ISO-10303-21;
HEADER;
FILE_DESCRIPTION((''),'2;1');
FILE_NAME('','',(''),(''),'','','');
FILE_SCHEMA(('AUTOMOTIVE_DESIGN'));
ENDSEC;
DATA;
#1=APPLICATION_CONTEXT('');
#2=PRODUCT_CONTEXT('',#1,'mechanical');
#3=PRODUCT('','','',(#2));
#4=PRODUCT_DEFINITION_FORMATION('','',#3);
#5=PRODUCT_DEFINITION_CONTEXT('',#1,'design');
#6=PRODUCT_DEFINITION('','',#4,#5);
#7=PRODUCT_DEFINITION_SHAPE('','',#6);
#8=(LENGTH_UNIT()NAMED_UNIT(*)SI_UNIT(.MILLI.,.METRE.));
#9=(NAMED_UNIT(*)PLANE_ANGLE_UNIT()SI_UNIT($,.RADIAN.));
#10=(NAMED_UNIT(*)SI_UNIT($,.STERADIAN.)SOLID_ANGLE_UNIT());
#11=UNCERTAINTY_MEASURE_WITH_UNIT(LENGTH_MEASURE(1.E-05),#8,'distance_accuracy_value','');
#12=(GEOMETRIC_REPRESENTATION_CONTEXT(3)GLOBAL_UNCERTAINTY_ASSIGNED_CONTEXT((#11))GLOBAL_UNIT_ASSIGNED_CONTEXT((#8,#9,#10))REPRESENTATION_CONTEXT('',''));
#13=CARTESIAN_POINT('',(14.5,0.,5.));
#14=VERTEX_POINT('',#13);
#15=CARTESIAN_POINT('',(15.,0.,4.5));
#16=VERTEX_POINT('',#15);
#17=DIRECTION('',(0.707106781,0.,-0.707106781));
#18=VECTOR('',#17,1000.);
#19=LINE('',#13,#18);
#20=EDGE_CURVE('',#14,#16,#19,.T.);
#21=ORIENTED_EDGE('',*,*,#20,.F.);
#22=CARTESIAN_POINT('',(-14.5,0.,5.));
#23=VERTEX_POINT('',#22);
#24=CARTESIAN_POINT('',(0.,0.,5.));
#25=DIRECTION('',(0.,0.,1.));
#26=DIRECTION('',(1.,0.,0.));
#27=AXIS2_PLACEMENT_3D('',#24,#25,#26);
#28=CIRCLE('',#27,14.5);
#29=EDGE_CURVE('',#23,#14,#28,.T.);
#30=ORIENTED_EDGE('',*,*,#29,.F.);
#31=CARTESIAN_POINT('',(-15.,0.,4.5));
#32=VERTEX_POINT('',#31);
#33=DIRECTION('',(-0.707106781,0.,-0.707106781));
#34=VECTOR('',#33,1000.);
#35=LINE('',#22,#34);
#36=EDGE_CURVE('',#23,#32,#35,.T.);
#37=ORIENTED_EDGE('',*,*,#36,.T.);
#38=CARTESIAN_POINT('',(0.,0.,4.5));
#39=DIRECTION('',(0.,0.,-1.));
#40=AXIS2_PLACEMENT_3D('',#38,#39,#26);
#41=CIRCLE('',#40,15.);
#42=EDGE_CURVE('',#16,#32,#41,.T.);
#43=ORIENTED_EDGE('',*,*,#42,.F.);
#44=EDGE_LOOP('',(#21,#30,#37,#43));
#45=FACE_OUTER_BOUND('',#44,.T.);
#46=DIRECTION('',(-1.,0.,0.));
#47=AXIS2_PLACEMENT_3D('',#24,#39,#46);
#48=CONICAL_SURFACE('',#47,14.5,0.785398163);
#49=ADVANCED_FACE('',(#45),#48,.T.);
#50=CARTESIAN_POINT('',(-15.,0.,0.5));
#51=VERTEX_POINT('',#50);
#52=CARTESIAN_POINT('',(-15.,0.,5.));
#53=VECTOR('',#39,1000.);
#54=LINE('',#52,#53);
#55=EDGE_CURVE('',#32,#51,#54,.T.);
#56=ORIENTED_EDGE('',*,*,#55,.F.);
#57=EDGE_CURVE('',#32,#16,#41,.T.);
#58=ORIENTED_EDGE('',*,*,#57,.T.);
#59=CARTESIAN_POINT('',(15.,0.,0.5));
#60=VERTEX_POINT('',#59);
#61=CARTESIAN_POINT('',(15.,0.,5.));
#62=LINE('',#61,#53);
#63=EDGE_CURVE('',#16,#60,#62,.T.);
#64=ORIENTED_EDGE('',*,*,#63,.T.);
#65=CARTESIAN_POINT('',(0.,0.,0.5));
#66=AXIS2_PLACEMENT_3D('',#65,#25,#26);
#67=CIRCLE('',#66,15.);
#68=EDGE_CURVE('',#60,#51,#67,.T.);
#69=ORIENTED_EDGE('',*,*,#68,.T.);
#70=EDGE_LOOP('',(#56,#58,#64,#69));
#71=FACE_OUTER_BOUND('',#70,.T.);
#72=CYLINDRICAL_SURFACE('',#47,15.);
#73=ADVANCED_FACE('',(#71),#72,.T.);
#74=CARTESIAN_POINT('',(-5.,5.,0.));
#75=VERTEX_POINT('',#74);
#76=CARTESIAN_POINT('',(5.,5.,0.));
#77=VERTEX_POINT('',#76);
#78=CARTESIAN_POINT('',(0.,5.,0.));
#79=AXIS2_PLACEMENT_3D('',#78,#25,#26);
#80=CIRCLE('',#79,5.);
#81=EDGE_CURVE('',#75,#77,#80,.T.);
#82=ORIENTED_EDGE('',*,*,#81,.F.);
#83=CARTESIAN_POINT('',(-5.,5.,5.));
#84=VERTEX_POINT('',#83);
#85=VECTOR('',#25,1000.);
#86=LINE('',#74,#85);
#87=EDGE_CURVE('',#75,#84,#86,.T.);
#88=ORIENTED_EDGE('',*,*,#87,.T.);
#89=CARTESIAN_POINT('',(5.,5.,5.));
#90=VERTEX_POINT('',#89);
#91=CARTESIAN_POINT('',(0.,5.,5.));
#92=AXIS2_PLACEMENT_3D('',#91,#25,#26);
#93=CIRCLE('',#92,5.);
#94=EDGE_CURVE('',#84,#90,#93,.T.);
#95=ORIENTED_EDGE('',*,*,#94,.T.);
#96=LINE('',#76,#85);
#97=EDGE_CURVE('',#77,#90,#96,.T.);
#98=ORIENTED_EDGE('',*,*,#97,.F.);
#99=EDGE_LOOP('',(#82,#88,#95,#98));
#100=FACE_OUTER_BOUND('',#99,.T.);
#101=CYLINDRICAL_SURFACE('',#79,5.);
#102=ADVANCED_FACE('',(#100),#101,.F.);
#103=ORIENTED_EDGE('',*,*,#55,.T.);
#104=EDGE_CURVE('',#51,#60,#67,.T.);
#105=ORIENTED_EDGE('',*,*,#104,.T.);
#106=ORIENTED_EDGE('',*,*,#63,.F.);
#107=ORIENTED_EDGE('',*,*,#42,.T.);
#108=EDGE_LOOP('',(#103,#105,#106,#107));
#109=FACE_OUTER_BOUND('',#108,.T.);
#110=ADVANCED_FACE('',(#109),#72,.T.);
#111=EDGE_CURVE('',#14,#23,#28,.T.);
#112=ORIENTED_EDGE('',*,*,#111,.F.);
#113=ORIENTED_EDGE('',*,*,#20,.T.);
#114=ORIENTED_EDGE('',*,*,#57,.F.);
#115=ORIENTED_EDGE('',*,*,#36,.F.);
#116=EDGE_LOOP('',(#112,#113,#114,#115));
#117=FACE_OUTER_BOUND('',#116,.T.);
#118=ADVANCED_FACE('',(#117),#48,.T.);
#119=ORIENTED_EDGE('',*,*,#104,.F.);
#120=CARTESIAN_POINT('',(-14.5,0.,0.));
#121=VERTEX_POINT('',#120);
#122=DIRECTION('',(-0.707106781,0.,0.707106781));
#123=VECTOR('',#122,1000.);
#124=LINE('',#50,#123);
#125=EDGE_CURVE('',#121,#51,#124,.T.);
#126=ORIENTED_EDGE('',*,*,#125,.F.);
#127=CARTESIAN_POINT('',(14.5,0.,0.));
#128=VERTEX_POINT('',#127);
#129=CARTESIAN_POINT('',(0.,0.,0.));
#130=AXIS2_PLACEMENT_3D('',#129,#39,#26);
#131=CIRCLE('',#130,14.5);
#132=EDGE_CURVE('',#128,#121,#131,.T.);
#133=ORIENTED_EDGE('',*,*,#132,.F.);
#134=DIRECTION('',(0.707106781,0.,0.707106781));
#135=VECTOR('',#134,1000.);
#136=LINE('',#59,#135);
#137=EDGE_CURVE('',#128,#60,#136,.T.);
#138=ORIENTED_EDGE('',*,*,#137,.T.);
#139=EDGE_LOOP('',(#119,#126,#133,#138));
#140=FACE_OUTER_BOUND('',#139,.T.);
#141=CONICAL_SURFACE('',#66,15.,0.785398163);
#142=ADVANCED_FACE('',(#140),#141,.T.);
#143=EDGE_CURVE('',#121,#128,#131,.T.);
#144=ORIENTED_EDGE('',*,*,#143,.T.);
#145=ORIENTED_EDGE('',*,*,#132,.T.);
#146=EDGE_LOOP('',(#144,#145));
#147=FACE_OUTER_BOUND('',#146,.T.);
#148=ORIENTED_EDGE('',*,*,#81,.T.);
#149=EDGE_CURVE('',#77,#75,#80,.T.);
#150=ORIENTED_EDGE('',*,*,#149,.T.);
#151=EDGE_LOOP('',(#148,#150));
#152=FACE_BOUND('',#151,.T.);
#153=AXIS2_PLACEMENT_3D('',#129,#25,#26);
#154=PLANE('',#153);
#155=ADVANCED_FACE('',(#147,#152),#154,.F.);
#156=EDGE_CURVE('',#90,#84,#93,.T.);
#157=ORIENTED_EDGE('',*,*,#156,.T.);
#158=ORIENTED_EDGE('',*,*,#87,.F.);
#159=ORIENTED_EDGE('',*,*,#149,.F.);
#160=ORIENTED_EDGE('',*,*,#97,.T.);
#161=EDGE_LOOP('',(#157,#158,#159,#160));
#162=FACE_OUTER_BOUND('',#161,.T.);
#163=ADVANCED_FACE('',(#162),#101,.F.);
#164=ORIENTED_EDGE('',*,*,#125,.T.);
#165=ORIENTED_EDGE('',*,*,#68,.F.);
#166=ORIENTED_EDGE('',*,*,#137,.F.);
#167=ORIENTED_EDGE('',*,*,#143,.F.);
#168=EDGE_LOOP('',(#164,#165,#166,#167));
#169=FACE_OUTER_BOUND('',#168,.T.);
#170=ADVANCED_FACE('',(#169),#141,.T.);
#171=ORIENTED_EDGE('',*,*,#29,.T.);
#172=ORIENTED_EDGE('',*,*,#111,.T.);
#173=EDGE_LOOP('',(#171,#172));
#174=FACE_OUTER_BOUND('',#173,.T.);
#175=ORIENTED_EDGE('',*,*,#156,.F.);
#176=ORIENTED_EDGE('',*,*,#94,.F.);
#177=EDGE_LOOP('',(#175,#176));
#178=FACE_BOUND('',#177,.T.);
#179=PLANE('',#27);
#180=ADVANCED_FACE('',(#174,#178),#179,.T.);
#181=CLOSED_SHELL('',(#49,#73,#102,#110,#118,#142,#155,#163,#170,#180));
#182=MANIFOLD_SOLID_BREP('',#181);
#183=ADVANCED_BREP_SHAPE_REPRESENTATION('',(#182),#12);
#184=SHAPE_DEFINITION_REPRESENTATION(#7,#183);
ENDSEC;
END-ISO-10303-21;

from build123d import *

# Parameters (mm, degrees)
SKETCH1_R           = 15
BOSS_EXTRUDE1_DEPTH = 5
SKETCH2_R           = 5
CUT_EXTRUDE1_DEPTH  = 5
CHAMFER1_SIZE       = 0.5


with BuildPart() as part:
    # Sketch1 → Boss-Extrude1 (new body)
    with BuildSketch(Plane.XY):
        Circle(SKETCH1_R)
    extrude(amount=BOSS_EXTRUDE1_DEPTH)

    # Sketch2 → Cut-Extrude1 (cut)
    with BuildSketch(Plane.XY.offset(5)):
        with Locations((0, 5)):
            Circle(SKETCH2_R)
    extrude(amount=-CUT_EXTRUDE1_DEPTH, mode=Mode.SUBTRACT)

    # Chamfer1
    chamfer1_edges = [part.edges().sort_by_distance(p)[0] for p in [
        (-15, 0, 0),
        (-15, 0, 5),
    ]]
    chamfer(chamfer1_edges, length=CHAMFER1_SIZE)


solid = part.part
